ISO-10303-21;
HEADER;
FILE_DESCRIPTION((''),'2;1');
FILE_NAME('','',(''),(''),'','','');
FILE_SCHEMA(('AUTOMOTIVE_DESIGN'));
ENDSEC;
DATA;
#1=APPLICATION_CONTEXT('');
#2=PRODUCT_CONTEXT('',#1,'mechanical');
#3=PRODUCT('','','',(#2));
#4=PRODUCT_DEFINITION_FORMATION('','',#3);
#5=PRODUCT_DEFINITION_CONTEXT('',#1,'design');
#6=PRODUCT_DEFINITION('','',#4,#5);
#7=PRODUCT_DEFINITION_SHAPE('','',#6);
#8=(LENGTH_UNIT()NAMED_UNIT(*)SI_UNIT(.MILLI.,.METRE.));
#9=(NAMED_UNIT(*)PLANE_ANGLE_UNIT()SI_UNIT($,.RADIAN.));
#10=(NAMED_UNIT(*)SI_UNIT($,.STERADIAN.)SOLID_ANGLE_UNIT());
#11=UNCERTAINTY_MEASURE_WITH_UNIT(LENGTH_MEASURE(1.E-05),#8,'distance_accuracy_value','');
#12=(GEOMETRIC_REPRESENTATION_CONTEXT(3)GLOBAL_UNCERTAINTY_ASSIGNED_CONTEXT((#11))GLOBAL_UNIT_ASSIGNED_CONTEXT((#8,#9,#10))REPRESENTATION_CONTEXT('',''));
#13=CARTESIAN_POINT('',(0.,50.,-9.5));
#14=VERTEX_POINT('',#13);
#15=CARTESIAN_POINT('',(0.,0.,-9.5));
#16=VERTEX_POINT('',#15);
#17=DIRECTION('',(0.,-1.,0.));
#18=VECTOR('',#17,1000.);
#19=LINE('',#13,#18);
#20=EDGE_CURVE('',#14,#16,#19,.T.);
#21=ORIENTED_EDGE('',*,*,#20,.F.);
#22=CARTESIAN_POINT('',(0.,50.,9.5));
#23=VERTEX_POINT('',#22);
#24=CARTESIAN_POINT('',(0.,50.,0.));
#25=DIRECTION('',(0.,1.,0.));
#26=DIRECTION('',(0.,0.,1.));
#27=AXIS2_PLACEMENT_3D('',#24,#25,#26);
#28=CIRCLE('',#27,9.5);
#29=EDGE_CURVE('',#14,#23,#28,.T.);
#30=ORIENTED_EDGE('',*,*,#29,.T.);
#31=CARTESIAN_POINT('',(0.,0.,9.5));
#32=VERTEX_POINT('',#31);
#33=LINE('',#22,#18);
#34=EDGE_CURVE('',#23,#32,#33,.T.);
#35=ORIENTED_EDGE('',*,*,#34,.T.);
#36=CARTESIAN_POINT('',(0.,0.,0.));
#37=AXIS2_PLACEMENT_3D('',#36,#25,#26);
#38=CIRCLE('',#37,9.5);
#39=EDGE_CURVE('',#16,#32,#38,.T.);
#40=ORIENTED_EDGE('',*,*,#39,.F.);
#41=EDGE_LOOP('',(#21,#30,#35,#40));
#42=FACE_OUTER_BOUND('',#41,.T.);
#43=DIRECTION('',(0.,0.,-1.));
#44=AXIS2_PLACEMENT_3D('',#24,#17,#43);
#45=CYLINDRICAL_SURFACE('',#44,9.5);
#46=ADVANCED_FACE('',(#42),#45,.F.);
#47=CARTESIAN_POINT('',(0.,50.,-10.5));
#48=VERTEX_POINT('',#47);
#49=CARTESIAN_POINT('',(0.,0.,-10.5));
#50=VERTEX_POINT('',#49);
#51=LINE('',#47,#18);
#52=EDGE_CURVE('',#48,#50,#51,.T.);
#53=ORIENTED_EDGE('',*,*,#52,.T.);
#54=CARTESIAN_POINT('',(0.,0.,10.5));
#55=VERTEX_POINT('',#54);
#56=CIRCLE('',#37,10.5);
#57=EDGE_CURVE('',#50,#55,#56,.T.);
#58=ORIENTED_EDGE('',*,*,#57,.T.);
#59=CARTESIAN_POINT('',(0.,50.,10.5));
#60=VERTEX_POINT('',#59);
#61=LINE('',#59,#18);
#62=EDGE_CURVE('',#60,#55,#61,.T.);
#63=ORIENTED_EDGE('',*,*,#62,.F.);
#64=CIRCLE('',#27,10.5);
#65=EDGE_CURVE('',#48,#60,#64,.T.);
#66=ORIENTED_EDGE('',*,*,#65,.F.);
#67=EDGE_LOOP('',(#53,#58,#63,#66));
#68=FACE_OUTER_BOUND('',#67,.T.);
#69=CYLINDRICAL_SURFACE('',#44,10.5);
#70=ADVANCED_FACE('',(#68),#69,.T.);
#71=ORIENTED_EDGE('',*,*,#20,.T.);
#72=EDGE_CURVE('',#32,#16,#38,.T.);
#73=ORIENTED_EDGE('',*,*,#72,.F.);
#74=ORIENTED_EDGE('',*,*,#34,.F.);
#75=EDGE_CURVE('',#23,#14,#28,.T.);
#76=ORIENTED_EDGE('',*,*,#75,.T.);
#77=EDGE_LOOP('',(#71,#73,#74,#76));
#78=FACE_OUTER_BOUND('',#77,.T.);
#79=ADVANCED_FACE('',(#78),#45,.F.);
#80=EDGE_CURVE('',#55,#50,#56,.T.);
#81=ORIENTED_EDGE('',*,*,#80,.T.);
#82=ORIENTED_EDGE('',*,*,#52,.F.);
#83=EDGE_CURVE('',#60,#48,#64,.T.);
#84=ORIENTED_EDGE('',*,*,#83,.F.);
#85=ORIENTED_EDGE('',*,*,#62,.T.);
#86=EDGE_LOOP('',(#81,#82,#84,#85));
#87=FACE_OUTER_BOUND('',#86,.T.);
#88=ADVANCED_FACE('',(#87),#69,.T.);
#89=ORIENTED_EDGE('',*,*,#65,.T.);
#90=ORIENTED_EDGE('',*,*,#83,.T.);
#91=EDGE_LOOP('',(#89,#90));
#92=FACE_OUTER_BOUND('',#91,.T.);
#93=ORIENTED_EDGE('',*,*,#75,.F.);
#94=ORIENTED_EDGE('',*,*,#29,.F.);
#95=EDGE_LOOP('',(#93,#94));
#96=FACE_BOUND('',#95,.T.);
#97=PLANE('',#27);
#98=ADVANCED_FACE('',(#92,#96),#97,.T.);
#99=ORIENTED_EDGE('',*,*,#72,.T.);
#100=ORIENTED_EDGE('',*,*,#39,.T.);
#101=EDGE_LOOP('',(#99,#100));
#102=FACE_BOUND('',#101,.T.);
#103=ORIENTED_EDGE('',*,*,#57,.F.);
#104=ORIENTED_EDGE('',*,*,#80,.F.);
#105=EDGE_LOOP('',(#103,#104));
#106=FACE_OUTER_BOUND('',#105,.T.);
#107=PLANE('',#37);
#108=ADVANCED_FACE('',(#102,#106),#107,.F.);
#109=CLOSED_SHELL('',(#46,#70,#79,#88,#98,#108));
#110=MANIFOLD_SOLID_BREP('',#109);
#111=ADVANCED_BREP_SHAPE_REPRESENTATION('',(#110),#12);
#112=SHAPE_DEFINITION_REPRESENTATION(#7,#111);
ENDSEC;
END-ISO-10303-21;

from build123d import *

# Parameters (mm, degrees)
SKETCH1_R           = 10.5
SKETCH1_R_2         = 9.5
BOSS_EXTRUDE1_DEPTH = 50


with BuildPart() as part:
    # Sketch1 → Boss-Extrude1 (new body)
    with BuildSketch(Plane(origin=(0, 0, 0), x_dir=(1, 0, 0), z_dir=(0, 1, 0))):
        with Locations(Location((0, 0, 0), (0, 0, 270))):
            Circle(SKETCH1_R)
        with Locations(Location((0, 0, 0), (0, 0, 270))):
            Circle(SKETCH1_R_2, mode=Mode.SUBTRACT)
    extrude(amount=BOSS_EXTRUDE1_DEPTH)


solid = part.part
